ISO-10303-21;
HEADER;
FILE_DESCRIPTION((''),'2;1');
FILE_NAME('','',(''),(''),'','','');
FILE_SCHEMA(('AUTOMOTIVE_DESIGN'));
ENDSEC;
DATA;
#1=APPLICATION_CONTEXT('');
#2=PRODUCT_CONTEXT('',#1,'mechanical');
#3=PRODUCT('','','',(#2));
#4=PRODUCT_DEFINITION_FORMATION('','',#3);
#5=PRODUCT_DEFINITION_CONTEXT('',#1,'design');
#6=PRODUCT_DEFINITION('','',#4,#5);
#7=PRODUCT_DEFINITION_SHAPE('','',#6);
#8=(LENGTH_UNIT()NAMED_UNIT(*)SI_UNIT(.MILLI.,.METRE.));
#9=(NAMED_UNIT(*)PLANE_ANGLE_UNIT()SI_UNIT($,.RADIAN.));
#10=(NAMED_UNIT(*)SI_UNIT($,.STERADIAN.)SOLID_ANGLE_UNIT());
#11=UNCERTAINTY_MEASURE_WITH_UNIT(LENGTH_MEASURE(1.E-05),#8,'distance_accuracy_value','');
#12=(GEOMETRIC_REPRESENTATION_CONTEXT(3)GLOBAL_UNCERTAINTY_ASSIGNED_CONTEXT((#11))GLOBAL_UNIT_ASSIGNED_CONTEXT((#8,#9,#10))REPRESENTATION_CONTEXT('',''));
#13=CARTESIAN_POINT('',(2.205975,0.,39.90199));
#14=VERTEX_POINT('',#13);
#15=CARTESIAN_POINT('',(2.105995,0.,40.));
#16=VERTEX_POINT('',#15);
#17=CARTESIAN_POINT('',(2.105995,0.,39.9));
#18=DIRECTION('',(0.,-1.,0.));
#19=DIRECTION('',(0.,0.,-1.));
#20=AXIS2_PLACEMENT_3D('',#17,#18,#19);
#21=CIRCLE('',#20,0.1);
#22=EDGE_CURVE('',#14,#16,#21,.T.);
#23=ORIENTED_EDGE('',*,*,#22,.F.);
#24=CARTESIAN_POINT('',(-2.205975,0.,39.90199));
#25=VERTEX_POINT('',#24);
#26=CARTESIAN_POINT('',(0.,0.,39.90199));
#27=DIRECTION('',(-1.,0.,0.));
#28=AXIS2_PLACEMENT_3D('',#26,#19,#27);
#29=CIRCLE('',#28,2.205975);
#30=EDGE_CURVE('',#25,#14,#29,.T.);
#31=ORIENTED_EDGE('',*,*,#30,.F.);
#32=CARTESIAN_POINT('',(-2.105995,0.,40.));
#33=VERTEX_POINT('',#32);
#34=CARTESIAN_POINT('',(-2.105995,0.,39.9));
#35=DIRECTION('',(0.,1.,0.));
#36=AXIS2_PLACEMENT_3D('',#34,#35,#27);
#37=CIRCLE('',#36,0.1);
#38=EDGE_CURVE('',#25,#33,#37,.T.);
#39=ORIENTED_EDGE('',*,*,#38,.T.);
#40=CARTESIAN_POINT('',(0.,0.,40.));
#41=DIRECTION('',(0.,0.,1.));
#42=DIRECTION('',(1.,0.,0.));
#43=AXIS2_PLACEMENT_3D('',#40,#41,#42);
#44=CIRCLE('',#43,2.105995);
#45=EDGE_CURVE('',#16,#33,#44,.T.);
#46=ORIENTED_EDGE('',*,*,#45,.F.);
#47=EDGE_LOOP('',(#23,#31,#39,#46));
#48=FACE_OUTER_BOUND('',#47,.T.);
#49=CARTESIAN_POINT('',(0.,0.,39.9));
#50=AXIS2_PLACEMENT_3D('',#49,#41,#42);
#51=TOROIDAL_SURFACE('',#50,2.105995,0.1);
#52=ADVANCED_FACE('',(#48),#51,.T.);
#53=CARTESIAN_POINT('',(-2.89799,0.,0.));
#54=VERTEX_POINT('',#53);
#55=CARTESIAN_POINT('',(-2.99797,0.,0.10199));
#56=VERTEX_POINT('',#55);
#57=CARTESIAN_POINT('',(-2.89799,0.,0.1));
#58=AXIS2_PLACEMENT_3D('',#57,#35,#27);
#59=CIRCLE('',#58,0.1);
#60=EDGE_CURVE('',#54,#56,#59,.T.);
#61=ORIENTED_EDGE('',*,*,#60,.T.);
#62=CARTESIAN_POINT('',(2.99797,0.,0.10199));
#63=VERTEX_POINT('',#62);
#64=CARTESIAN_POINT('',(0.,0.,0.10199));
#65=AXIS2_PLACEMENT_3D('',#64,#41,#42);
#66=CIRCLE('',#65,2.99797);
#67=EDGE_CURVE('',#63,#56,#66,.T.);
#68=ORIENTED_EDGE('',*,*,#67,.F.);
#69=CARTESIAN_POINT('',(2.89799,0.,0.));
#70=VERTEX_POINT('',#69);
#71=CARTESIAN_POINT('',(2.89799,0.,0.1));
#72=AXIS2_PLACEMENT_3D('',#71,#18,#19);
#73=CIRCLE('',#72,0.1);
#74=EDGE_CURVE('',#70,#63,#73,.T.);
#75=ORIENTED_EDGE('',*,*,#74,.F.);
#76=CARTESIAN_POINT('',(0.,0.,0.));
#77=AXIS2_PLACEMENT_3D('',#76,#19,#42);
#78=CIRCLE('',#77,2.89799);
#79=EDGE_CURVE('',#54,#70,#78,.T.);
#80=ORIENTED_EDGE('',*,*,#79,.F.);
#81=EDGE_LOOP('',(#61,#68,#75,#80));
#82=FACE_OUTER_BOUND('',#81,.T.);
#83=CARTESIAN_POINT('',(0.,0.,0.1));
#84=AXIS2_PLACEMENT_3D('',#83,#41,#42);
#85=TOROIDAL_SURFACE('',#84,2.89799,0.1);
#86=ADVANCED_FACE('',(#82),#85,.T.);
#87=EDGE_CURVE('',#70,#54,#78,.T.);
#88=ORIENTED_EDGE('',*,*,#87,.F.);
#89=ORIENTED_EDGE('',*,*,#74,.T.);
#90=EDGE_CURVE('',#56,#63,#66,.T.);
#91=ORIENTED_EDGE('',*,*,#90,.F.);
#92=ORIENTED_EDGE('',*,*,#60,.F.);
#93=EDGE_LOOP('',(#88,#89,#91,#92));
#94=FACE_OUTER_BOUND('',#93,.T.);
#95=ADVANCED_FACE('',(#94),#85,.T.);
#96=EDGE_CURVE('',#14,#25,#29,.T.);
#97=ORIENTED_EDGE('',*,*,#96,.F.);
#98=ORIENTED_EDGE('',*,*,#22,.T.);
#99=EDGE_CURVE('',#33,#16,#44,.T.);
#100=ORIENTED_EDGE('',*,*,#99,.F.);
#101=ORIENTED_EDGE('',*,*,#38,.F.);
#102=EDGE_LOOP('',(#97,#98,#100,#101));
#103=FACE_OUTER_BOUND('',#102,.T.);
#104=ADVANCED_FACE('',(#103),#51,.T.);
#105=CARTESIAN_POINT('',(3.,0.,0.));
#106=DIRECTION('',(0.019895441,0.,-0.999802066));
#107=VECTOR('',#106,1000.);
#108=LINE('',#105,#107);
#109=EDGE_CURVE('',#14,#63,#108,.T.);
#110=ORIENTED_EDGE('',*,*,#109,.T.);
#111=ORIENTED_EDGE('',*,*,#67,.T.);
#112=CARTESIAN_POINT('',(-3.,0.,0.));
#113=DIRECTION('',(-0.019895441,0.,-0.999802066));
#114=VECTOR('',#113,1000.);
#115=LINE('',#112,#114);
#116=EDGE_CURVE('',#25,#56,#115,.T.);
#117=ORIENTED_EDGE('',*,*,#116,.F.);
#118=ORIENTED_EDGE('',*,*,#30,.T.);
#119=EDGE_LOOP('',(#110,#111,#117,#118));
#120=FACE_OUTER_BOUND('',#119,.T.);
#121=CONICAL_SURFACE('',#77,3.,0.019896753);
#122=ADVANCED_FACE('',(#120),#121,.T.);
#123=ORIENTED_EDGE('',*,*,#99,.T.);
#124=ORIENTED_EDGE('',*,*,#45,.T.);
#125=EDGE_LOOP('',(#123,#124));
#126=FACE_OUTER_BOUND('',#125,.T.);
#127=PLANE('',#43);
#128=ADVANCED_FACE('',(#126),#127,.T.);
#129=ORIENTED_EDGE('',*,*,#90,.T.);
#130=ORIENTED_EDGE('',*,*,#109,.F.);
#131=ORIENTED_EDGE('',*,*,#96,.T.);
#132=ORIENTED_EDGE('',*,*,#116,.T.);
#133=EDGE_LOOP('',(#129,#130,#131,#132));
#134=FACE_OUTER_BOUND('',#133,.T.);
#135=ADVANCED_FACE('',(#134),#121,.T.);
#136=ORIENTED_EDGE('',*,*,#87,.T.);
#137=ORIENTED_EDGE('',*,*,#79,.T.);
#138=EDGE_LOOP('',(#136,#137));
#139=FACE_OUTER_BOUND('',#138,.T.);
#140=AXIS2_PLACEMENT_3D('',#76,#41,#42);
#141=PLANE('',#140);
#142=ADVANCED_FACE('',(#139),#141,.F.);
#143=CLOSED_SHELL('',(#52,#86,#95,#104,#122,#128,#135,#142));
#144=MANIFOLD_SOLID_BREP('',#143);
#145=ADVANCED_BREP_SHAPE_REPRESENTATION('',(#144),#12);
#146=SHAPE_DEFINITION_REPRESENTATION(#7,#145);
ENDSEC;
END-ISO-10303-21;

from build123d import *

# Parameters (mm, degrees)
SKETCH_1_R      = 3
EXTRUDE_1_DEPTH = 40
EXTRUDE_1_TAPER = 1.14
FILLET_1_R      = 0.1


with BuildPart() as part:
    # 草图1 → 凸台-拉伸1 (new body)
    with BuildSketch(Plane.XY):
        Circle(SKETCH_1_R)
    extrude(amount=EXTRUDE_1_DEPTH, taper=EXTRUDE_1_TAPER)

    # 圆角1
    fillet_1_edges = [part.edges().sort_by_distance(p)[0] for p in [
        (-3, 0, 0),
        (-2.204024821, 0, 40),
    ]]
    fillet(fillet_1_edges, radius=FILLET_1_R)


solid = part.part
